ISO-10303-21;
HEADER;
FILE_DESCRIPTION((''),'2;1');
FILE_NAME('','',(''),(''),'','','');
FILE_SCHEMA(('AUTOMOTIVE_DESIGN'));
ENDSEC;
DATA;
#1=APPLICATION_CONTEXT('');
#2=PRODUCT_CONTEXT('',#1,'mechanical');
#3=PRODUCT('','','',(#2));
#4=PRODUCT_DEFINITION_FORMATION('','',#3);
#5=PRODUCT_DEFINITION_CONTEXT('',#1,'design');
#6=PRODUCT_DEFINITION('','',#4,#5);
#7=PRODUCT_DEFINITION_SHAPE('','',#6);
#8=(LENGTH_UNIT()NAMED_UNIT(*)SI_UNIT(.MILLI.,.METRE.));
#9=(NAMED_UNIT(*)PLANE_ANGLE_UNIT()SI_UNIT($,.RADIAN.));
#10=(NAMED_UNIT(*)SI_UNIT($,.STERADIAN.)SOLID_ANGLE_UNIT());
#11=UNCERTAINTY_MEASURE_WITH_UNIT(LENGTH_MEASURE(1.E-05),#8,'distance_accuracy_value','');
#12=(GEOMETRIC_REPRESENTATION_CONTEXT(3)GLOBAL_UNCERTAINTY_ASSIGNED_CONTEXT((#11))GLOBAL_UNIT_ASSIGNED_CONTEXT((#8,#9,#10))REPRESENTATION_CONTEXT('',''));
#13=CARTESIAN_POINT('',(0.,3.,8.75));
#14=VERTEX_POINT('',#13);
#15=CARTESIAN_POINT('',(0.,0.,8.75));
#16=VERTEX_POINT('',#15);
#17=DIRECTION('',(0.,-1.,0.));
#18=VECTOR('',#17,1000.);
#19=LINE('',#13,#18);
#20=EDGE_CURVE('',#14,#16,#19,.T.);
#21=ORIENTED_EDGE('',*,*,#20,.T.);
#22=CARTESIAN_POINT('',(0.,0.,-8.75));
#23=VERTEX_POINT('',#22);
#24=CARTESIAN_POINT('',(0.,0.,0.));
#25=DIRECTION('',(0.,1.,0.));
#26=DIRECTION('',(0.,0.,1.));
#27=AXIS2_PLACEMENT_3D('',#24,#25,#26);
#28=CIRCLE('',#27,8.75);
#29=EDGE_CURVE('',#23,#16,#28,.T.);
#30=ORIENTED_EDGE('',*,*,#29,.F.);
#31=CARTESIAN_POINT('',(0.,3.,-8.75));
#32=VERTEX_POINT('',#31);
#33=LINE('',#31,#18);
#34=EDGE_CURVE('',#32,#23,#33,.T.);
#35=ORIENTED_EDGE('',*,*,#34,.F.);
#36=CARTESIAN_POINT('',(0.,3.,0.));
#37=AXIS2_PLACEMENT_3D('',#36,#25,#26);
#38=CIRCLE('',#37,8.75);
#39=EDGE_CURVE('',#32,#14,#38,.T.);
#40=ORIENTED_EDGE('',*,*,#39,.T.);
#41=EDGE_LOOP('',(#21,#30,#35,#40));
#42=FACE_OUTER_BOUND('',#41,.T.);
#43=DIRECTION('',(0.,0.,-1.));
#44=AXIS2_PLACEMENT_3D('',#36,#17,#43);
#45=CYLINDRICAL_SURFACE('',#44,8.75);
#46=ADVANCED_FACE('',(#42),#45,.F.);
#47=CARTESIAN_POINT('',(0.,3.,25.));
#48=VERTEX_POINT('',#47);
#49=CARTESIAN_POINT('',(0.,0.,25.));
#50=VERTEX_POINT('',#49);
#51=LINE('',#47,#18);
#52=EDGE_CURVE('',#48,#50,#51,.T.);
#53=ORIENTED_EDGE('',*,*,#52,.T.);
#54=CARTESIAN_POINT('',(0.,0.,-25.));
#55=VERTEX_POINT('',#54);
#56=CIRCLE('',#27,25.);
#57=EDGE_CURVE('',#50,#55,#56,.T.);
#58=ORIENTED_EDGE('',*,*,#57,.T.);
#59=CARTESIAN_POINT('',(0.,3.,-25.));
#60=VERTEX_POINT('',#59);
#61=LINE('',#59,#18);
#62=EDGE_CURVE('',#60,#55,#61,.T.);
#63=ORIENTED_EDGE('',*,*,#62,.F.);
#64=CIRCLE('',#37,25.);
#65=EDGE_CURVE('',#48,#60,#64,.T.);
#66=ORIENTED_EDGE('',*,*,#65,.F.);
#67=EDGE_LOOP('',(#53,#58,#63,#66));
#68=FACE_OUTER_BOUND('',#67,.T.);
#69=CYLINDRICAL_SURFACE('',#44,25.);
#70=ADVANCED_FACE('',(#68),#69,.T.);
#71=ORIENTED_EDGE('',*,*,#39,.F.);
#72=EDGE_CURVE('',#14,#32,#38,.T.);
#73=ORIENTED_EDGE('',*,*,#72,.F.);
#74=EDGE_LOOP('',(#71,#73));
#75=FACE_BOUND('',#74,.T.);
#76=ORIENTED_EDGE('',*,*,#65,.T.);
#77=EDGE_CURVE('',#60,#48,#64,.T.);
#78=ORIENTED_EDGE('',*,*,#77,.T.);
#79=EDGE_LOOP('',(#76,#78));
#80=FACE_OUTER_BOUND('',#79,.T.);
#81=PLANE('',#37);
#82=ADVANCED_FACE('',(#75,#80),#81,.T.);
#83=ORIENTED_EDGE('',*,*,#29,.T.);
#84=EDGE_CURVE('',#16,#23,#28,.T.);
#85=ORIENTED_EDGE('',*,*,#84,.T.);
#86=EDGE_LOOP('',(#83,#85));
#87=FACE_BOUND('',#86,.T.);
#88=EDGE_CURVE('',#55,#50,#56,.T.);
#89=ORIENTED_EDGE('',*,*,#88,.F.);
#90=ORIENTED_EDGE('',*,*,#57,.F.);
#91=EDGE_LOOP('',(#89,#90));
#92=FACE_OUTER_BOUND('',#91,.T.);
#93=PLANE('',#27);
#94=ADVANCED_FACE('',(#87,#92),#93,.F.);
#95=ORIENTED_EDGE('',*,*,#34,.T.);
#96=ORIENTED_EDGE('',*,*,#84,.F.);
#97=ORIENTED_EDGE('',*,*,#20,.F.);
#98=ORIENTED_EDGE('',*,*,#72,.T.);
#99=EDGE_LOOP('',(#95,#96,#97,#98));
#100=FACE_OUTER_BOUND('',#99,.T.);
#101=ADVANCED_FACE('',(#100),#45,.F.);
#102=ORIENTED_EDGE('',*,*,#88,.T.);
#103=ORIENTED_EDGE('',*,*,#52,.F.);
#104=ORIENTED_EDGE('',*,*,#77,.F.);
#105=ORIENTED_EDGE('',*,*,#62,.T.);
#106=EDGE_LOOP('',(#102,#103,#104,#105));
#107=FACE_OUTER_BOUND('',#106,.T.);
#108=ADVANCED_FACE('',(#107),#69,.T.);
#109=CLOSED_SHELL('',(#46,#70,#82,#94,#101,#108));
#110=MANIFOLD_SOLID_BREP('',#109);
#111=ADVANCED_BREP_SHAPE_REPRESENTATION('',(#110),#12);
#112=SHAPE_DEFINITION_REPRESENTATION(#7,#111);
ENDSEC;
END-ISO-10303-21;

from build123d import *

# Parameters (mm, degrees)
SKETCH1_R           = 25
SKETCH1_R_2         = 8.75
BOSS_EXTRUDE1_DEPTH = 3


with BuildPart() as part:
    # Sketch1 → Boss-Extrude1 (new body)
    with BuildSketch(Plane(origin=(0, 0, 0), x_dir=(1, 0, 0), z_dir=(0, 1, 0))):
        with Locations(Location((0, 0, 0), (0, 0, 270))):
            Circle(SKETCH1_R)
        with Locations(Location((0, 0, 0), (0, 0, 270))):
            Circle(SKETCH1_R_2, mode=Mode.SUBTRACT)
    extrude(amount=BOSS_EXTRUDE1_DEPTH)


solid = part.part
